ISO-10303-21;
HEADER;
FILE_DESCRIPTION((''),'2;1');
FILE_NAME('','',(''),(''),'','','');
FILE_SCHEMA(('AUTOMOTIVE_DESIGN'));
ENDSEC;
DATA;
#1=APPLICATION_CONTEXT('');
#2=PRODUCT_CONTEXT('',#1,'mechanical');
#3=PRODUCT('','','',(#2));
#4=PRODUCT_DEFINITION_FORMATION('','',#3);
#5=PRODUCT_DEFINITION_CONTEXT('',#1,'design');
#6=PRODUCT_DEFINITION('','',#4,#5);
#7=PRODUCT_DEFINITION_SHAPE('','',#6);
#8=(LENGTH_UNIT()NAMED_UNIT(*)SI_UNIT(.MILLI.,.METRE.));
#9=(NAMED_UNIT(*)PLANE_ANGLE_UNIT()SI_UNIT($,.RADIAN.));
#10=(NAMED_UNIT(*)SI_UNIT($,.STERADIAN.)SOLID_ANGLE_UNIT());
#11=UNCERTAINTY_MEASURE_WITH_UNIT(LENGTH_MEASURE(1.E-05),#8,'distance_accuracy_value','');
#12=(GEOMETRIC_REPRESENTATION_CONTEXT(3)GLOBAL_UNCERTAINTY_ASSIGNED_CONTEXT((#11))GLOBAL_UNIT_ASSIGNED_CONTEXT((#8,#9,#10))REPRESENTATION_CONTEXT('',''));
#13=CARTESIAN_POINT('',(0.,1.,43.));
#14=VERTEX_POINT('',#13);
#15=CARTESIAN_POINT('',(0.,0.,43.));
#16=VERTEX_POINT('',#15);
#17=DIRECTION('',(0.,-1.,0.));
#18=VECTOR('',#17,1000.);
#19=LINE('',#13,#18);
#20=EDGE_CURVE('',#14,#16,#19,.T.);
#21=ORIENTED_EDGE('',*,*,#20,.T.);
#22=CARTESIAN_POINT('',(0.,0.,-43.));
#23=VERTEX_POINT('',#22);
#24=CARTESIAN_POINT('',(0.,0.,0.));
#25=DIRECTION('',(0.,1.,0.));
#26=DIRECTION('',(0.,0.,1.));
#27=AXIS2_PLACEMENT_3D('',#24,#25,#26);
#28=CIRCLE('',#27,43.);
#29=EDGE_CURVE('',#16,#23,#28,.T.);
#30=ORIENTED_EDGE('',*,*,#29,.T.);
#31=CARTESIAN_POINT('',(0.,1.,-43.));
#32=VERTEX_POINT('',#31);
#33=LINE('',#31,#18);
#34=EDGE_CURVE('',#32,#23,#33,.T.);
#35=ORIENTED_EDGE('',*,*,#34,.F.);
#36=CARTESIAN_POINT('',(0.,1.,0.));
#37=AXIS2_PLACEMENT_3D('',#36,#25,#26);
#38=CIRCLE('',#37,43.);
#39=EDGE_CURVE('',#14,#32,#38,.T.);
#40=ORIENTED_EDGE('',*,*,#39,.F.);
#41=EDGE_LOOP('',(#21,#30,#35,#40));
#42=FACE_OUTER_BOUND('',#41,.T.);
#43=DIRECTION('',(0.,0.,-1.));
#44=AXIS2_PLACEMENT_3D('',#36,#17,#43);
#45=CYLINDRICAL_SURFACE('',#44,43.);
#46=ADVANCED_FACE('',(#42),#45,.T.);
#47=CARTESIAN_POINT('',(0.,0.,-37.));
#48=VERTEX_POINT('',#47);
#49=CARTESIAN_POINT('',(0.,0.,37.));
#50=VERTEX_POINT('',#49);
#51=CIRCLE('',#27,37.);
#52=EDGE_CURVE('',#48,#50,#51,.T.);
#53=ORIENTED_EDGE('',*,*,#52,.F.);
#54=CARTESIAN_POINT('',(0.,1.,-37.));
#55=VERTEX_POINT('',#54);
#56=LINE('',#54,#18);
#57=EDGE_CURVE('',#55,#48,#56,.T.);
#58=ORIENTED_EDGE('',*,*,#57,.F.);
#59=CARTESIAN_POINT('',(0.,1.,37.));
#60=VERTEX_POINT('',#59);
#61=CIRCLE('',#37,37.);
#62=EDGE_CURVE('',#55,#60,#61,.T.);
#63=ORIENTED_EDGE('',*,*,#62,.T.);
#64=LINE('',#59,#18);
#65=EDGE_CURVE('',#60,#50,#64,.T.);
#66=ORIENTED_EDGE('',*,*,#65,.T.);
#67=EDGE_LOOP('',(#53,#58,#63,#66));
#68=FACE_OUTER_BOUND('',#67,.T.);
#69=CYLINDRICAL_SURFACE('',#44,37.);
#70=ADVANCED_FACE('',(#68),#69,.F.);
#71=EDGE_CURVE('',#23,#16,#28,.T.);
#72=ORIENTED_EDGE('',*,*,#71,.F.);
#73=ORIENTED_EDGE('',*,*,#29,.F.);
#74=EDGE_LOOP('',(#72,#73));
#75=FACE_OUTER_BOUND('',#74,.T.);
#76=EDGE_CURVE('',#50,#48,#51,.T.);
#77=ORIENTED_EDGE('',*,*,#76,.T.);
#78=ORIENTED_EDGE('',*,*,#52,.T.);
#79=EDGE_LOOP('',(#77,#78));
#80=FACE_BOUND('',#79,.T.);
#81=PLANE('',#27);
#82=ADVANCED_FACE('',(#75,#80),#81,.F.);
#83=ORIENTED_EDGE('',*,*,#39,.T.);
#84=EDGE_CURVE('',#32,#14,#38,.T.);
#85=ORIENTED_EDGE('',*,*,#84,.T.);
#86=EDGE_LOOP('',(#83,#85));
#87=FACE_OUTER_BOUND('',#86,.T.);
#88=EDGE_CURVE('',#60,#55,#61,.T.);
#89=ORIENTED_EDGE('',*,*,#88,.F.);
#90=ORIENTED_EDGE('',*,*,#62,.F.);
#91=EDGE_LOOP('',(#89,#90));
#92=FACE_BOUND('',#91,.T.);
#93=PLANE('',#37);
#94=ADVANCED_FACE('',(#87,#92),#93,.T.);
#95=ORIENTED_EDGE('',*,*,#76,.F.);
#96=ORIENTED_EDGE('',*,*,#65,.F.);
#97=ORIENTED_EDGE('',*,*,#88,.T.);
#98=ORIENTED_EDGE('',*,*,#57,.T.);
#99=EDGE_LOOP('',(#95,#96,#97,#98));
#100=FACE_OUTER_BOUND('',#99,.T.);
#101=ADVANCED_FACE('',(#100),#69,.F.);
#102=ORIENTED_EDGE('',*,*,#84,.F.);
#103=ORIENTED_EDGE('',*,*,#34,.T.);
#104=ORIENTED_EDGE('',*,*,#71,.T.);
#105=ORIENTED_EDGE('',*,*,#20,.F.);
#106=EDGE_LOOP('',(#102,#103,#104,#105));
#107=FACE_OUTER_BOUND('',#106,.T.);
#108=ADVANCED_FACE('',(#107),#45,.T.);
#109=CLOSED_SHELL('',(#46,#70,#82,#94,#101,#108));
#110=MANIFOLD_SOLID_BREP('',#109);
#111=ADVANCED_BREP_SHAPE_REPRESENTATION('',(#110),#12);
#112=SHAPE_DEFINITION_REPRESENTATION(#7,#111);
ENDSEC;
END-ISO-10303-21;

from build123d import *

# Parameters (mm, degrees)
SKETCH1_R           = 43
SKETCH1_R_2         = 37
BOSS_EXTRUDE1_DEPTH = 1


with BuildPart() as part:
    # Sketch1 → Boss-Extrude1 (new body)
    with BuildSketch(Plane(origin=(0, 0, 0), x_dir=(1, 0, 0), z_dir=(0, 1, 0))):
        with Locations(Location((0, 0, 0), (0, 0, 270))):
            Circle(SKETCH1_R)
        with Locations(Location((0, 0, 0), (0, 0, 270))):
            Circle(SKETCH1_R_2, mode=Mode.SUBTRACT)
    extrude(amount=BOSS_EXTRUDE1_DEPTH)


solid = part.part
